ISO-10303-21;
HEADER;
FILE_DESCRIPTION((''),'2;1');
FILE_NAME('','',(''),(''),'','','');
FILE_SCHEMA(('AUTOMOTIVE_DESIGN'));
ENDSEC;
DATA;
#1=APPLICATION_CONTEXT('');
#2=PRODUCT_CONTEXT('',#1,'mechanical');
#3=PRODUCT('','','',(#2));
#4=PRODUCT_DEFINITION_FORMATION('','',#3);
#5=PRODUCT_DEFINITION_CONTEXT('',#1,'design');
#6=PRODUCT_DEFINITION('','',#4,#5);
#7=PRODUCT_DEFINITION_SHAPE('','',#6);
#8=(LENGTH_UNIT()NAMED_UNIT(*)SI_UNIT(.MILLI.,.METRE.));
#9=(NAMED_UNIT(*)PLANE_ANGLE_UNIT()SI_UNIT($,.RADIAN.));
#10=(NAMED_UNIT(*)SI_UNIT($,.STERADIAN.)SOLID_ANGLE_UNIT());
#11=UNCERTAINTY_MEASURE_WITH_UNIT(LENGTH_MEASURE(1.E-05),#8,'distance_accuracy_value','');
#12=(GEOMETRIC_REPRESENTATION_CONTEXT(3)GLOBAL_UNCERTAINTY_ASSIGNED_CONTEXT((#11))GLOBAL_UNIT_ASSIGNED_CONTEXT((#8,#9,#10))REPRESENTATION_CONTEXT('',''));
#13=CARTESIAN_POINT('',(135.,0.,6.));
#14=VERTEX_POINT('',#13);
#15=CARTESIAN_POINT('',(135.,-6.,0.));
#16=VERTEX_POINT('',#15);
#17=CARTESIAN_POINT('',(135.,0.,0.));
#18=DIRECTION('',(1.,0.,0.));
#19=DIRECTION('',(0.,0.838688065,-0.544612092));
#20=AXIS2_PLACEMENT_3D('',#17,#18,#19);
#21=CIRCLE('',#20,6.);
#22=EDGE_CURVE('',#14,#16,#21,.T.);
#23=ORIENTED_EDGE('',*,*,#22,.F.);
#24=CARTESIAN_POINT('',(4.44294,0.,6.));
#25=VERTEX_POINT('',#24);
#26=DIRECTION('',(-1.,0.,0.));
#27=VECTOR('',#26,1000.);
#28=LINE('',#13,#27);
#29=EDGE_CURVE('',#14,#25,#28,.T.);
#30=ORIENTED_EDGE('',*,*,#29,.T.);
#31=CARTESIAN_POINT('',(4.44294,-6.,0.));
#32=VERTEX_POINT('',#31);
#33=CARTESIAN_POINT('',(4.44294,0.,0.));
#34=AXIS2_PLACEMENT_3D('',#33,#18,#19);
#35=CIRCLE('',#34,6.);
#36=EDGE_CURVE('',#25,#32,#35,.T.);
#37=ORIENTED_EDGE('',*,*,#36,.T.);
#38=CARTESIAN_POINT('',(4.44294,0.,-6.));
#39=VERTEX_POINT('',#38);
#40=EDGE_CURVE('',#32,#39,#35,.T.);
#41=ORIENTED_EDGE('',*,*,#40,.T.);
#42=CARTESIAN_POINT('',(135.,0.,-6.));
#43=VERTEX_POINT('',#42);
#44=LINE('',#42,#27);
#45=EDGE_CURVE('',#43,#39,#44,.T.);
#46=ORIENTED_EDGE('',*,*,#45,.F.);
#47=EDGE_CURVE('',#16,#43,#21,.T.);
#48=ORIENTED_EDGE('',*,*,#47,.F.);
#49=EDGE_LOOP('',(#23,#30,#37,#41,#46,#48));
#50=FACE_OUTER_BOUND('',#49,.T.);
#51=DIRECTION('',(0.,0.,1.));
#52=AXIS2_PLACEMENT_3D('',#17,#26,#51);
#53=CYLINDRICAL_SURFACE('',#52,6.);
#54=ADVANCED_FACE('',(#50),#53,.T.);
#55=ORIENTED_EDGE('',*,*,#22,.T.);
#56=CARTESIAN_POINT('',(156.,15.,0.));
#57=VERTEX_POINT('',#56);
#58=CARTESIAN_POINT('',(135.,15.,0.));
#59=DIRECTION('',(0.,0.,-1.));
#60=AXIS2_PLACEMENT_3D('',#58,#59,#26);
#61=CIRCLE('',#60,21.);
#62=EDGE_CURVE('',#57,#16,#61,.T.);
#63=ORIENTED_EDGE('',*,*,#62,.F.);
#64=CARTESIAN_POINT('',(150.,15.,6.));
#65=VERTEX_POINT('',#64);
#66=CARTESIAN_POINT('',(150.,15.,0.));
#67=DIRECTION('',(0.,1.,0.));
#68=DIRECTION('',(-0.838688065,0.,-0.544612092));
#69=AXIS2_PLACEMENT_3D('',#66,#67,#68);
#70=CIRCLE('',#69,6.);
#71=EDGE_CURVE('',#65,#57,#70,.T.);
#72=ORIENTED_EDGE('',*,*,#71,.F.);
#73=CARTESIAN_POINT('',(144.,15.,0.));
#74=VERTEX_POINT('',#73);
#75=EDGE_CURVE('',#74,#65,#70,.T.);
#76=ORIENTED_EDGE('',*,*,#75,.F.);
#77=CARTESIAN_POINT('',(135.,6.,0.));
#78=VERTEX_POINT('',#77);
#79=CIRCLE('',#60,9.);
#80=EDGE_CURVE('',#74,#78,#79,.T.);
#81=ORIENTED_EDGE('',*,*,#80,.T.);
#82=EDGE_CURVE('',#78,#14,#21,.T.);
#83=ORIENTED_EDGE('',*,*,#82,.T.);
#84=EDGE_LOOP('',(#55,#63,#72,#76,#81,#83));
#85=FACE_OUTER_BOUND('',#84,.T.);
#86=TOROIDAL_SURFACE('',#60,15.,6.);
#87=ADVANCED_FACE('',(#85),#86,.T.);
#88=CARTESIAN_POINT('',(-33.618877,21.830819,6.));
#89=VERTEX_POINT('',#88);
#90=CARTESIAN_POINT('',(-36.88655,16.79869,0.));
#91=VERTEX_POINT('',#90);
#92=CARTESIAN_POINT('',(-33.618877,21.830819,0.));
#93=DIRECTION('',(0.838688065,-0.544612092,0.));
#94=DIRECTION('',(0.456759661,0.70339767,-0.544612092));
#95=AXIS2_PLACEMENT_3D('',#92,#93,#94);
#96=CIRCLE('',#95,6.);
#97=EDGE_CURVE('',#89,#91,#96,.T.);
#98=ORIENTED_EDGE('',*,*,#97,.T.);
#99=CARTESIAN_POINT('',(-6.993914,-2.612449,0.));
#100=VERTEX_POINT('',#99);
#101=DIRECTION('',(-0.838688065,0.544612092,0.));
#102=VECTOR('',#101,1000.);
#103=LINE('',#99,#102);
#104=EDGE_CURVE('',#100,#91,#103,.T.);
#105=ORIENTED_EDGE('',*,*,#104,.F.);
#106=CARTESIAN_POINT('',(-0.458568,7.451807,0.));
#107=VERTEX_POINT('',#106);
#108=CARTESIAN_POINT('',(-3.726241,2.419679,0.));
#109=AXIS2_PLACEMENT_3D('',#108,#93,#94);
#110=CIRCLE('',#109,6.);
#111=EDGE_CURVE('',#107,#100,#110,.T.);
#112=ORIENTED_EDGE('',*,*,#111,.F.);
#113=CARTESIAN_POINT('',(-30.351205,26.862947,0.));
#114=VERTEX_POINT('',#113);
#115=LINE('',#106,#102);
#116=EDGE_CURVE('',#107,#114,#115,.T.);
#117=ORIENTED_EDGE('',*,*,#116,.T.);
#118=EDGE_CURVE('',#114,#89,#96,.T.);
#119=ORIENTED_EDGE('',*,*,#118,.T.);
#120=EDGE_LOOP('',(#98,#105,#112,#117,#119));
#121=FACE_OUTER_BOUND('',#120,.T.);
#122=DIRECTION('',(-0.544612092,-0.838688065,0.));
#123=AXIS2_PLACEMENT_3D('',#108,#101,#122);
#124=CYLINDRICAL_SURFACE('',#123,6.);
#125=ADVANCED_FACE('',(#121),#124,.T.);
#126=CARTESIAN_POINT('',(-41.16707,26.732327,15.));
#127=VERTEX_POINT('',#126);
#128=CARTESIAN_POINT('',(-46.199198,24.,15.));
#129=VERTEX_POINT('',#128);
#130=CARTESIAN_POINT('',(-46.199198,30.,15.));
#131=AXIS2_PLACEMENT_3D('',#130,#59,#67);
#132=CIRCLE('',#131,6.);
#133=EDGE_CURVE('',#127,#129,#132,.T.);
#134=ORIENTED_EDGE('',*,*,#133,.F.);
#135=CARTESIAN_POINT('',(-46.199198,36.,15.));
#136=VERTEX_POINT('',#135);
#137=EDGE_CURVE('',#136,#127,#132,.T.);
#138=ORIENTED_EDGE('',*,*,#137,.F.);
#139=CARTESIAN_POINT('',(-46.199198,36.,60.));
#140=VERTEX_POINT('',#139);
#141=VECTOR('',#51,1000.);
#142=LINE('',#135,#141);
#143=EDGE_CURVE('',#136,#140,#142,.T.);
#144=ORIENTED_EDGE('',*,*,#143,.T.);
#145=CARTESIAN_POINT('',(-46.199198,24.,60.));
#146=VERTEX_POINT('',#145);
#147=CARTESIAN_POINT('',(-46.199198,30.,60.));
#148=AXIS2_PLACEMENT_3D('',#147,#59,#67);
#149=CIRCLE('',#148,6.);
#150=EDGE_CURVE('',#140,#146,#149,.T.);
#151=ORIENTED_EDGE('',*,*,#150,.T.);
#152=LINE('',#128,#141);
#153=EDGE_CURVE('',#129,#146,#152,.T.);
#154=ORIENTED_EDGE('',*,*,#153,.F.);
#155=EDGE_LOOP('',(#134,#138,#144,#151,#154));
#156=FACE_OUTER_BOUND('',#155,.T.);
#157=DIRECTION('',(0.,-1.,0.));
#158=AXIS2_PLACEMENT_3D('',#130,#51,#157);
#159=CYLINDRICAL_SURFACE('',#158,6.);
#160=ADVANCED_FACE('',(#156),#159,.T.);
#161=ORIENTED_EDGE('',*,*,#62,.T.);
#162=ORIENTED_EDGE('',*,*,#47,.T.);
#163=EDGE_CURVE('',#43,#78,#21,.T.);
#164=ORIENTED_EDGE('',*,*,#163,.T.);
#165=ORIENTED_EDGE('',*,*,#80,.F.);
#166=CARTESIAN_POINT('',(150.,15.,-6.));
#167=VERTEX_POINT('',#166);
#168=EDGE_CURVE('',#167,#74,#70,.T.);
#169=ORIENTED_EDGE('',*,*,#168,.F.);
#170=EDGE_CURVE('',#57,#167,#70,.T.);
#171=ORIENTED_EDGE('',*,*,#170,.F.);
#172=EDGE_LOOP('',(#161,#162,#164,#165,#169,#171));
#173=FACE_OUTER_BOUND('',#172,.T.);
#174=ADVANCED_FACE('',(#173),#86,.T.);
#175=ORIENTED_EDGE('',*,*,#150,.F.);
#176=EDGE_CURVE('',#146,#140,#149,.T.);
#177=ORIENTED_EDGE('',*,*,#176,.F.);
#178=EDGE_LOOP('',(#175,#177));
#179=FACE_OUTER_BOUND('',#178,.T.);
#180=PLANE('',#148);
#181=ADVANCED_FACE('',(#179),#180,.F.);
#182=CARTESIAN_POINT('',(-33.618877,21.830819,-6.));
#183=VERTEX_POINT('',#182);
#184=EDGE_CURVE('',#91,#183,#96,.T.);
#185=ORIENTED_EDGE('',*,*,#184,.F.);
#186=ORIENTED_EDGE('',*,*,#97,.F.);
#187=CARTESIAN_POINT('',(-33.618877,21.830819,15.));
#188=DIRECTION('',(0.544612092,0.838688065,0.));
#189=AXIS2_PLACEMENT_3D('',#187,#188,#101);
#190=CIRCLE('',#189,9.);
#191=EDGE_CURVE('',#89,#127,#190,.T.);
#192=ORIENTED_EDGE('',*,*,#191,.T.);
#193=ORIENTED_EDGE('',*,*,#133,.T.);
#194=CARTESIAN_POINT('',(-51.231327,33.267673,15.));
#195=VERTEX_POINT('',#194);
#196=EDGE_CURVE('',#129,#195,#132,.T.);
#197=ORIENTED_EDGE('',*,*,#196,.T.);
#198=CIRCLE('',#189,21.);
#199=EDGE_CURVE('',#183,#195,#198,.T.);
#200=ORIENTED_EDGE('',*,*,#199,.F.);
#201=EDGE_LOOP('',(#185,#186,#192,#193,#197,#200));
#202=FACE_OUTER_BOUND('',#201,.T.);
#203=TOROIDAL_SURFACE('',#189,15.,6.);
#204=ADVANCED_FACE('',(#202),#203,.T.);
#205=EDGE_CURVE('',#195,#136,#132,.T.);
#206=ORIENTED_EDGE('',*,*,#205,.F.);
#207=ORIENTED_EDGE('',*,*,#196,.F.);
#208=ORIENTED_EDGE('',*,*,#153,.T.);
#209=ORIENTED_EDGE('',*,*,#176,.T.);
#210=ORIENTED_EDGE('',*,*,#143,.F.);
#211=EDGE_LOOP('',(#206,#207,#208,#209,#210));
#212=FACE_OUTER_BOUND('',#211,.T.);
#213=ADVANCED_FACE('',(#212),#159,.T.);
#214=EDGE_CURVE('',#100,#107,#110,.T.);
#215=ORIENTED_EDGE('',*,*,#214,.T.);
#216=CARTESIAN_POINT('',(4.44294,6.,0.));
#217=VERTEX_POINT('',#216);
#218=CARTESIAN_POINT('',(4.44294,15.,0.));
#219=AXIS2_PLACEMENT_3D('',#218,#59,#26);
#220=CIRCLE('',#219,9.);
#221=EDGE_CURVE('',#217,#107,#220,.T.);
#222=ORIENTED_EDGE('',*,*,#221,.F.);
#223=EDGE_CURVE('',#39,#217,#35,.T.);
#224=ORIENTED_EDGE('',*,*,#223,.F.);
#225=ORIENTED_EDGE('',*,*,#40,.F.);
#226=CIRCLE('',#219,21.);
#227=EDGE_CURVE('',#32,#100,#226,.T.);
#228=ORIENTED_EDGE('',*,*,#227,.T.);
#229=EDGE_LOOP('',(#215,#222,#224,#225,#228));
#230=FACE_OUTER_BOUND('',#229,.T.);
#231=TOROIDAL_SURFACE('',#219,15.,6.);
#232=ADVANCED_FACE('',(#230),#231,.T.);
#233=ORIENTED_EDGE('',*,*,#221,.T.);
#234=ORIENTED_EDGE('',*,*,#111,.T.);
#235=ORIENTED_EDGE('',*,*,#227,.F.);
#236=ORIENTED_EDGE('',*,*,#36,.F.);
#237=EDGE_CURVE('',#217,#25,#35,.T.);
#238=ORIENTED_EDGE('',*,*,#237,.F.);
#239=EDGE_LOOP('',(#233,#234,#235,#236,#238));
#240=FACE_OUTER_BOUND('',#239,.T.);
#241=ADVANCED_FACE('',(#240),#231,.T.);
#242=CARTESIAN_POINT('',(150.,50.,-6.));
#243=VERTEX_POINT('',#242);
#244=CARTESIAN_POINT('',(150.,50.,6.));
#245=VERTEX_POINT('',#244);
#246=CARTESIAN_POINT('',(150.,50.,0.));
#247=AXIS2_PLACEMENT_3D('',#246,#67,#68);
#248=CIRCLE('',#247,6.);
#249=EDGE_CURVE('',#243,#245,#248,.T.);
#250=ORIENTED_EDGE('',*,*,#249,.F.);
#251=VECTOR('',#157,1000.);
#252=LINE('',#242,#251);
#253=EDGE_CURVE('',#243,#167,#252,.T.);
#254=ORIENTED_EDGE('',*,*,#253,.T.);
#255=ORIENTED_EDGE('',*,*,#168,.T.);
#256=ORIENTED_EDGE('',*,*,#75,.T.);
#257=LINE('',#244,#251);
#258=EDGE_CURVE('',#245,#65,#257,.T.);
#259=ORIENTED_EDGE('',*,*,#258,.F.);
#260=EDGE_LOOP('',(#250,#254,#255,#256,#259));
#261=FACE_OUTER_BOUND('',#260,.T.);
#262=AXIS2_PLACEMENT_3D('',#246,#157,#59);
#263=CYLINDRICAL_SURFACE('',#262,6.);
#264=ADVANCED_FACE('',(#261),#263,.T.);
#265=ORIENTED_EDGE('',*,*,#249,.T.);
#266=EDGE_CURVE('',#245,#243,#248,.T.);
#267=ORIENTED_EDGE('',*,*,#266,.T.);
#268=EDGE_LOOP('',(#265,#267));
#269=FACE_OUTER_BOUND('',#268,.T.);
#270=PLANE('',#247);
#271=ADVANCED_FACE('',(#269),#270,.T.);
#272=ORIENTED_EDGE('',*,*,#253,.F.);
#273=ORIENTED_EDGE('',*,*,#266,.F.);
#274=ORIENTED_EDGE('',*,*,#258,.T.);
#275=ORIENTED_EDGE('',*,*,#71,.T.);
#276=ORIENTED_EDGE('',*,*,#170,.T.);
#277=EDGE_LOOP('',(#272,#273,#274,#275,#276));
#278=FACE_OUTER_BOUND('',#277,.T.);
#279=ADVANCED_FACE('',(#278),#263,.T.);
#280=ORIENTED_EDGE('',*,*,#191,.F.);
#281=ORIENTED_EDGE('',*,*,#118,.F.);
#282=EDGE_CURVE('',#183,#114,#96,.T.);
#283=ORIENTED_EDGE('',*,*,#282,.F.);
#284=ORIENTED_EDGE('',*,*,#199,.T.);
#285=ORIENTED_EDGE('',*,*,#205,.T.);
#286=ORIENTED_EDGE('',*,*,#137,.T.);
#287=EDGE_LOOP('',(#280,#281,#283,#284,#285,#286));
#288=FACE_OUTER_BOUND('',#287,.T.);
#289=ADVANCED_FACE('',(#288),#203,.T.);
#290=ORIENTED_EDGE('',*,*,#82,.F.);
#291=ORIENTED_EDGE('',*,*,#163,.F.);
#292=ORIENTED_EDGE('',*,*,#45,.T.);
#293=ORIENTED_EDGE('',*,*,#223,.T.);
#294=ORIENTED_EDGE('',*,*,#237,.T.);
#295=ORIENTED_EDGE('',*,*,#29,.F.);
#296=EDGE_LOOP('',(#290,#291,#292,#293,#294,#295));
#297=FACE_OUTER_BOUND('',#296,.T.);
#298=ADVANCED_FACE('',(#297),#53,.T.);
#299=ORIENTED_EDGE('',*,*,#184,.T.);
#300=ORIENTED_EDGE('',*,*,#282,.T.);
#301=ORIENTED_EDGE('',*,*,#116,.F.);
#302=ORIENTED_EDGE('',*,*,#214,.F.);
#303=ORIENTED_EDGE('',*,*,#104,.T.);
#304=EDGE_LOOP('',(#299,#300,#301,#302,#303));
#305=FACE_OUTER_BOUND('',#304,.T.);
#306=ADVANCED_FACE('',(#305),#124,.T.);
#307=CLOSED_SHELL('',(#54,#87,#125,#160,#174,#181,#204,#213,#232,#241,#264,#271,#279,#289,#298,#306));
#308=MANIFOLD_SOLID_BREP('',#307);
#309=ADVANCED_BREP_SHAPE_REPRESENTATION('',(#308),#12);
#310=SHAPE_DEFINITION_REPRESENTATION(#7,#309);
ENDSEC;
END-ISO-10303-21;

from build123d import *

# Parameters (mm, degrees)
SWEEP_1_PROFILE_R = 6


with BuildPart() as part:
    # 扫描1: sweep along a curve in space
    with BuildLine() as sweep_1_path:
        Line((150, 15, 0), (150, 50, 0))
        ThreePointArc((135, 0, 0), (145.606601718, 4.393398282, 0), (150, 15, 0))
        Line((4.442940339, 0, 0), (135, 0, 0))
        ThreePointArc((4.442940339, 0, 0), (0.182941192, 0.617635547, 0), (-3.726241034, 2.41967903, 0))
        Line((-3.726241034, 2.41967903, 0), (-33.618877196, 21.830818627, 0))
        ThreePointArc((-33.618877196, 21.830818627, 0), (-42.514507463, 27.607302173, 4.393398282), (-46.199198166, 30, 15))
        Line((-46.199198166, 30, 15), (-46.199198166, 30, 60))
    # 扫描1 profile (on start of the path) → 扫描1 (sweep)
    with BuildSketch(Plane(origin=(-46.199198166, 30, 60), x_dir=(0, -1, 0), z_dir=(0, 0, -1))):
        Circle(SWEEP_1_PROFILE_R)
    sweep(path=sweep_1_path.line)


solid = part.part
